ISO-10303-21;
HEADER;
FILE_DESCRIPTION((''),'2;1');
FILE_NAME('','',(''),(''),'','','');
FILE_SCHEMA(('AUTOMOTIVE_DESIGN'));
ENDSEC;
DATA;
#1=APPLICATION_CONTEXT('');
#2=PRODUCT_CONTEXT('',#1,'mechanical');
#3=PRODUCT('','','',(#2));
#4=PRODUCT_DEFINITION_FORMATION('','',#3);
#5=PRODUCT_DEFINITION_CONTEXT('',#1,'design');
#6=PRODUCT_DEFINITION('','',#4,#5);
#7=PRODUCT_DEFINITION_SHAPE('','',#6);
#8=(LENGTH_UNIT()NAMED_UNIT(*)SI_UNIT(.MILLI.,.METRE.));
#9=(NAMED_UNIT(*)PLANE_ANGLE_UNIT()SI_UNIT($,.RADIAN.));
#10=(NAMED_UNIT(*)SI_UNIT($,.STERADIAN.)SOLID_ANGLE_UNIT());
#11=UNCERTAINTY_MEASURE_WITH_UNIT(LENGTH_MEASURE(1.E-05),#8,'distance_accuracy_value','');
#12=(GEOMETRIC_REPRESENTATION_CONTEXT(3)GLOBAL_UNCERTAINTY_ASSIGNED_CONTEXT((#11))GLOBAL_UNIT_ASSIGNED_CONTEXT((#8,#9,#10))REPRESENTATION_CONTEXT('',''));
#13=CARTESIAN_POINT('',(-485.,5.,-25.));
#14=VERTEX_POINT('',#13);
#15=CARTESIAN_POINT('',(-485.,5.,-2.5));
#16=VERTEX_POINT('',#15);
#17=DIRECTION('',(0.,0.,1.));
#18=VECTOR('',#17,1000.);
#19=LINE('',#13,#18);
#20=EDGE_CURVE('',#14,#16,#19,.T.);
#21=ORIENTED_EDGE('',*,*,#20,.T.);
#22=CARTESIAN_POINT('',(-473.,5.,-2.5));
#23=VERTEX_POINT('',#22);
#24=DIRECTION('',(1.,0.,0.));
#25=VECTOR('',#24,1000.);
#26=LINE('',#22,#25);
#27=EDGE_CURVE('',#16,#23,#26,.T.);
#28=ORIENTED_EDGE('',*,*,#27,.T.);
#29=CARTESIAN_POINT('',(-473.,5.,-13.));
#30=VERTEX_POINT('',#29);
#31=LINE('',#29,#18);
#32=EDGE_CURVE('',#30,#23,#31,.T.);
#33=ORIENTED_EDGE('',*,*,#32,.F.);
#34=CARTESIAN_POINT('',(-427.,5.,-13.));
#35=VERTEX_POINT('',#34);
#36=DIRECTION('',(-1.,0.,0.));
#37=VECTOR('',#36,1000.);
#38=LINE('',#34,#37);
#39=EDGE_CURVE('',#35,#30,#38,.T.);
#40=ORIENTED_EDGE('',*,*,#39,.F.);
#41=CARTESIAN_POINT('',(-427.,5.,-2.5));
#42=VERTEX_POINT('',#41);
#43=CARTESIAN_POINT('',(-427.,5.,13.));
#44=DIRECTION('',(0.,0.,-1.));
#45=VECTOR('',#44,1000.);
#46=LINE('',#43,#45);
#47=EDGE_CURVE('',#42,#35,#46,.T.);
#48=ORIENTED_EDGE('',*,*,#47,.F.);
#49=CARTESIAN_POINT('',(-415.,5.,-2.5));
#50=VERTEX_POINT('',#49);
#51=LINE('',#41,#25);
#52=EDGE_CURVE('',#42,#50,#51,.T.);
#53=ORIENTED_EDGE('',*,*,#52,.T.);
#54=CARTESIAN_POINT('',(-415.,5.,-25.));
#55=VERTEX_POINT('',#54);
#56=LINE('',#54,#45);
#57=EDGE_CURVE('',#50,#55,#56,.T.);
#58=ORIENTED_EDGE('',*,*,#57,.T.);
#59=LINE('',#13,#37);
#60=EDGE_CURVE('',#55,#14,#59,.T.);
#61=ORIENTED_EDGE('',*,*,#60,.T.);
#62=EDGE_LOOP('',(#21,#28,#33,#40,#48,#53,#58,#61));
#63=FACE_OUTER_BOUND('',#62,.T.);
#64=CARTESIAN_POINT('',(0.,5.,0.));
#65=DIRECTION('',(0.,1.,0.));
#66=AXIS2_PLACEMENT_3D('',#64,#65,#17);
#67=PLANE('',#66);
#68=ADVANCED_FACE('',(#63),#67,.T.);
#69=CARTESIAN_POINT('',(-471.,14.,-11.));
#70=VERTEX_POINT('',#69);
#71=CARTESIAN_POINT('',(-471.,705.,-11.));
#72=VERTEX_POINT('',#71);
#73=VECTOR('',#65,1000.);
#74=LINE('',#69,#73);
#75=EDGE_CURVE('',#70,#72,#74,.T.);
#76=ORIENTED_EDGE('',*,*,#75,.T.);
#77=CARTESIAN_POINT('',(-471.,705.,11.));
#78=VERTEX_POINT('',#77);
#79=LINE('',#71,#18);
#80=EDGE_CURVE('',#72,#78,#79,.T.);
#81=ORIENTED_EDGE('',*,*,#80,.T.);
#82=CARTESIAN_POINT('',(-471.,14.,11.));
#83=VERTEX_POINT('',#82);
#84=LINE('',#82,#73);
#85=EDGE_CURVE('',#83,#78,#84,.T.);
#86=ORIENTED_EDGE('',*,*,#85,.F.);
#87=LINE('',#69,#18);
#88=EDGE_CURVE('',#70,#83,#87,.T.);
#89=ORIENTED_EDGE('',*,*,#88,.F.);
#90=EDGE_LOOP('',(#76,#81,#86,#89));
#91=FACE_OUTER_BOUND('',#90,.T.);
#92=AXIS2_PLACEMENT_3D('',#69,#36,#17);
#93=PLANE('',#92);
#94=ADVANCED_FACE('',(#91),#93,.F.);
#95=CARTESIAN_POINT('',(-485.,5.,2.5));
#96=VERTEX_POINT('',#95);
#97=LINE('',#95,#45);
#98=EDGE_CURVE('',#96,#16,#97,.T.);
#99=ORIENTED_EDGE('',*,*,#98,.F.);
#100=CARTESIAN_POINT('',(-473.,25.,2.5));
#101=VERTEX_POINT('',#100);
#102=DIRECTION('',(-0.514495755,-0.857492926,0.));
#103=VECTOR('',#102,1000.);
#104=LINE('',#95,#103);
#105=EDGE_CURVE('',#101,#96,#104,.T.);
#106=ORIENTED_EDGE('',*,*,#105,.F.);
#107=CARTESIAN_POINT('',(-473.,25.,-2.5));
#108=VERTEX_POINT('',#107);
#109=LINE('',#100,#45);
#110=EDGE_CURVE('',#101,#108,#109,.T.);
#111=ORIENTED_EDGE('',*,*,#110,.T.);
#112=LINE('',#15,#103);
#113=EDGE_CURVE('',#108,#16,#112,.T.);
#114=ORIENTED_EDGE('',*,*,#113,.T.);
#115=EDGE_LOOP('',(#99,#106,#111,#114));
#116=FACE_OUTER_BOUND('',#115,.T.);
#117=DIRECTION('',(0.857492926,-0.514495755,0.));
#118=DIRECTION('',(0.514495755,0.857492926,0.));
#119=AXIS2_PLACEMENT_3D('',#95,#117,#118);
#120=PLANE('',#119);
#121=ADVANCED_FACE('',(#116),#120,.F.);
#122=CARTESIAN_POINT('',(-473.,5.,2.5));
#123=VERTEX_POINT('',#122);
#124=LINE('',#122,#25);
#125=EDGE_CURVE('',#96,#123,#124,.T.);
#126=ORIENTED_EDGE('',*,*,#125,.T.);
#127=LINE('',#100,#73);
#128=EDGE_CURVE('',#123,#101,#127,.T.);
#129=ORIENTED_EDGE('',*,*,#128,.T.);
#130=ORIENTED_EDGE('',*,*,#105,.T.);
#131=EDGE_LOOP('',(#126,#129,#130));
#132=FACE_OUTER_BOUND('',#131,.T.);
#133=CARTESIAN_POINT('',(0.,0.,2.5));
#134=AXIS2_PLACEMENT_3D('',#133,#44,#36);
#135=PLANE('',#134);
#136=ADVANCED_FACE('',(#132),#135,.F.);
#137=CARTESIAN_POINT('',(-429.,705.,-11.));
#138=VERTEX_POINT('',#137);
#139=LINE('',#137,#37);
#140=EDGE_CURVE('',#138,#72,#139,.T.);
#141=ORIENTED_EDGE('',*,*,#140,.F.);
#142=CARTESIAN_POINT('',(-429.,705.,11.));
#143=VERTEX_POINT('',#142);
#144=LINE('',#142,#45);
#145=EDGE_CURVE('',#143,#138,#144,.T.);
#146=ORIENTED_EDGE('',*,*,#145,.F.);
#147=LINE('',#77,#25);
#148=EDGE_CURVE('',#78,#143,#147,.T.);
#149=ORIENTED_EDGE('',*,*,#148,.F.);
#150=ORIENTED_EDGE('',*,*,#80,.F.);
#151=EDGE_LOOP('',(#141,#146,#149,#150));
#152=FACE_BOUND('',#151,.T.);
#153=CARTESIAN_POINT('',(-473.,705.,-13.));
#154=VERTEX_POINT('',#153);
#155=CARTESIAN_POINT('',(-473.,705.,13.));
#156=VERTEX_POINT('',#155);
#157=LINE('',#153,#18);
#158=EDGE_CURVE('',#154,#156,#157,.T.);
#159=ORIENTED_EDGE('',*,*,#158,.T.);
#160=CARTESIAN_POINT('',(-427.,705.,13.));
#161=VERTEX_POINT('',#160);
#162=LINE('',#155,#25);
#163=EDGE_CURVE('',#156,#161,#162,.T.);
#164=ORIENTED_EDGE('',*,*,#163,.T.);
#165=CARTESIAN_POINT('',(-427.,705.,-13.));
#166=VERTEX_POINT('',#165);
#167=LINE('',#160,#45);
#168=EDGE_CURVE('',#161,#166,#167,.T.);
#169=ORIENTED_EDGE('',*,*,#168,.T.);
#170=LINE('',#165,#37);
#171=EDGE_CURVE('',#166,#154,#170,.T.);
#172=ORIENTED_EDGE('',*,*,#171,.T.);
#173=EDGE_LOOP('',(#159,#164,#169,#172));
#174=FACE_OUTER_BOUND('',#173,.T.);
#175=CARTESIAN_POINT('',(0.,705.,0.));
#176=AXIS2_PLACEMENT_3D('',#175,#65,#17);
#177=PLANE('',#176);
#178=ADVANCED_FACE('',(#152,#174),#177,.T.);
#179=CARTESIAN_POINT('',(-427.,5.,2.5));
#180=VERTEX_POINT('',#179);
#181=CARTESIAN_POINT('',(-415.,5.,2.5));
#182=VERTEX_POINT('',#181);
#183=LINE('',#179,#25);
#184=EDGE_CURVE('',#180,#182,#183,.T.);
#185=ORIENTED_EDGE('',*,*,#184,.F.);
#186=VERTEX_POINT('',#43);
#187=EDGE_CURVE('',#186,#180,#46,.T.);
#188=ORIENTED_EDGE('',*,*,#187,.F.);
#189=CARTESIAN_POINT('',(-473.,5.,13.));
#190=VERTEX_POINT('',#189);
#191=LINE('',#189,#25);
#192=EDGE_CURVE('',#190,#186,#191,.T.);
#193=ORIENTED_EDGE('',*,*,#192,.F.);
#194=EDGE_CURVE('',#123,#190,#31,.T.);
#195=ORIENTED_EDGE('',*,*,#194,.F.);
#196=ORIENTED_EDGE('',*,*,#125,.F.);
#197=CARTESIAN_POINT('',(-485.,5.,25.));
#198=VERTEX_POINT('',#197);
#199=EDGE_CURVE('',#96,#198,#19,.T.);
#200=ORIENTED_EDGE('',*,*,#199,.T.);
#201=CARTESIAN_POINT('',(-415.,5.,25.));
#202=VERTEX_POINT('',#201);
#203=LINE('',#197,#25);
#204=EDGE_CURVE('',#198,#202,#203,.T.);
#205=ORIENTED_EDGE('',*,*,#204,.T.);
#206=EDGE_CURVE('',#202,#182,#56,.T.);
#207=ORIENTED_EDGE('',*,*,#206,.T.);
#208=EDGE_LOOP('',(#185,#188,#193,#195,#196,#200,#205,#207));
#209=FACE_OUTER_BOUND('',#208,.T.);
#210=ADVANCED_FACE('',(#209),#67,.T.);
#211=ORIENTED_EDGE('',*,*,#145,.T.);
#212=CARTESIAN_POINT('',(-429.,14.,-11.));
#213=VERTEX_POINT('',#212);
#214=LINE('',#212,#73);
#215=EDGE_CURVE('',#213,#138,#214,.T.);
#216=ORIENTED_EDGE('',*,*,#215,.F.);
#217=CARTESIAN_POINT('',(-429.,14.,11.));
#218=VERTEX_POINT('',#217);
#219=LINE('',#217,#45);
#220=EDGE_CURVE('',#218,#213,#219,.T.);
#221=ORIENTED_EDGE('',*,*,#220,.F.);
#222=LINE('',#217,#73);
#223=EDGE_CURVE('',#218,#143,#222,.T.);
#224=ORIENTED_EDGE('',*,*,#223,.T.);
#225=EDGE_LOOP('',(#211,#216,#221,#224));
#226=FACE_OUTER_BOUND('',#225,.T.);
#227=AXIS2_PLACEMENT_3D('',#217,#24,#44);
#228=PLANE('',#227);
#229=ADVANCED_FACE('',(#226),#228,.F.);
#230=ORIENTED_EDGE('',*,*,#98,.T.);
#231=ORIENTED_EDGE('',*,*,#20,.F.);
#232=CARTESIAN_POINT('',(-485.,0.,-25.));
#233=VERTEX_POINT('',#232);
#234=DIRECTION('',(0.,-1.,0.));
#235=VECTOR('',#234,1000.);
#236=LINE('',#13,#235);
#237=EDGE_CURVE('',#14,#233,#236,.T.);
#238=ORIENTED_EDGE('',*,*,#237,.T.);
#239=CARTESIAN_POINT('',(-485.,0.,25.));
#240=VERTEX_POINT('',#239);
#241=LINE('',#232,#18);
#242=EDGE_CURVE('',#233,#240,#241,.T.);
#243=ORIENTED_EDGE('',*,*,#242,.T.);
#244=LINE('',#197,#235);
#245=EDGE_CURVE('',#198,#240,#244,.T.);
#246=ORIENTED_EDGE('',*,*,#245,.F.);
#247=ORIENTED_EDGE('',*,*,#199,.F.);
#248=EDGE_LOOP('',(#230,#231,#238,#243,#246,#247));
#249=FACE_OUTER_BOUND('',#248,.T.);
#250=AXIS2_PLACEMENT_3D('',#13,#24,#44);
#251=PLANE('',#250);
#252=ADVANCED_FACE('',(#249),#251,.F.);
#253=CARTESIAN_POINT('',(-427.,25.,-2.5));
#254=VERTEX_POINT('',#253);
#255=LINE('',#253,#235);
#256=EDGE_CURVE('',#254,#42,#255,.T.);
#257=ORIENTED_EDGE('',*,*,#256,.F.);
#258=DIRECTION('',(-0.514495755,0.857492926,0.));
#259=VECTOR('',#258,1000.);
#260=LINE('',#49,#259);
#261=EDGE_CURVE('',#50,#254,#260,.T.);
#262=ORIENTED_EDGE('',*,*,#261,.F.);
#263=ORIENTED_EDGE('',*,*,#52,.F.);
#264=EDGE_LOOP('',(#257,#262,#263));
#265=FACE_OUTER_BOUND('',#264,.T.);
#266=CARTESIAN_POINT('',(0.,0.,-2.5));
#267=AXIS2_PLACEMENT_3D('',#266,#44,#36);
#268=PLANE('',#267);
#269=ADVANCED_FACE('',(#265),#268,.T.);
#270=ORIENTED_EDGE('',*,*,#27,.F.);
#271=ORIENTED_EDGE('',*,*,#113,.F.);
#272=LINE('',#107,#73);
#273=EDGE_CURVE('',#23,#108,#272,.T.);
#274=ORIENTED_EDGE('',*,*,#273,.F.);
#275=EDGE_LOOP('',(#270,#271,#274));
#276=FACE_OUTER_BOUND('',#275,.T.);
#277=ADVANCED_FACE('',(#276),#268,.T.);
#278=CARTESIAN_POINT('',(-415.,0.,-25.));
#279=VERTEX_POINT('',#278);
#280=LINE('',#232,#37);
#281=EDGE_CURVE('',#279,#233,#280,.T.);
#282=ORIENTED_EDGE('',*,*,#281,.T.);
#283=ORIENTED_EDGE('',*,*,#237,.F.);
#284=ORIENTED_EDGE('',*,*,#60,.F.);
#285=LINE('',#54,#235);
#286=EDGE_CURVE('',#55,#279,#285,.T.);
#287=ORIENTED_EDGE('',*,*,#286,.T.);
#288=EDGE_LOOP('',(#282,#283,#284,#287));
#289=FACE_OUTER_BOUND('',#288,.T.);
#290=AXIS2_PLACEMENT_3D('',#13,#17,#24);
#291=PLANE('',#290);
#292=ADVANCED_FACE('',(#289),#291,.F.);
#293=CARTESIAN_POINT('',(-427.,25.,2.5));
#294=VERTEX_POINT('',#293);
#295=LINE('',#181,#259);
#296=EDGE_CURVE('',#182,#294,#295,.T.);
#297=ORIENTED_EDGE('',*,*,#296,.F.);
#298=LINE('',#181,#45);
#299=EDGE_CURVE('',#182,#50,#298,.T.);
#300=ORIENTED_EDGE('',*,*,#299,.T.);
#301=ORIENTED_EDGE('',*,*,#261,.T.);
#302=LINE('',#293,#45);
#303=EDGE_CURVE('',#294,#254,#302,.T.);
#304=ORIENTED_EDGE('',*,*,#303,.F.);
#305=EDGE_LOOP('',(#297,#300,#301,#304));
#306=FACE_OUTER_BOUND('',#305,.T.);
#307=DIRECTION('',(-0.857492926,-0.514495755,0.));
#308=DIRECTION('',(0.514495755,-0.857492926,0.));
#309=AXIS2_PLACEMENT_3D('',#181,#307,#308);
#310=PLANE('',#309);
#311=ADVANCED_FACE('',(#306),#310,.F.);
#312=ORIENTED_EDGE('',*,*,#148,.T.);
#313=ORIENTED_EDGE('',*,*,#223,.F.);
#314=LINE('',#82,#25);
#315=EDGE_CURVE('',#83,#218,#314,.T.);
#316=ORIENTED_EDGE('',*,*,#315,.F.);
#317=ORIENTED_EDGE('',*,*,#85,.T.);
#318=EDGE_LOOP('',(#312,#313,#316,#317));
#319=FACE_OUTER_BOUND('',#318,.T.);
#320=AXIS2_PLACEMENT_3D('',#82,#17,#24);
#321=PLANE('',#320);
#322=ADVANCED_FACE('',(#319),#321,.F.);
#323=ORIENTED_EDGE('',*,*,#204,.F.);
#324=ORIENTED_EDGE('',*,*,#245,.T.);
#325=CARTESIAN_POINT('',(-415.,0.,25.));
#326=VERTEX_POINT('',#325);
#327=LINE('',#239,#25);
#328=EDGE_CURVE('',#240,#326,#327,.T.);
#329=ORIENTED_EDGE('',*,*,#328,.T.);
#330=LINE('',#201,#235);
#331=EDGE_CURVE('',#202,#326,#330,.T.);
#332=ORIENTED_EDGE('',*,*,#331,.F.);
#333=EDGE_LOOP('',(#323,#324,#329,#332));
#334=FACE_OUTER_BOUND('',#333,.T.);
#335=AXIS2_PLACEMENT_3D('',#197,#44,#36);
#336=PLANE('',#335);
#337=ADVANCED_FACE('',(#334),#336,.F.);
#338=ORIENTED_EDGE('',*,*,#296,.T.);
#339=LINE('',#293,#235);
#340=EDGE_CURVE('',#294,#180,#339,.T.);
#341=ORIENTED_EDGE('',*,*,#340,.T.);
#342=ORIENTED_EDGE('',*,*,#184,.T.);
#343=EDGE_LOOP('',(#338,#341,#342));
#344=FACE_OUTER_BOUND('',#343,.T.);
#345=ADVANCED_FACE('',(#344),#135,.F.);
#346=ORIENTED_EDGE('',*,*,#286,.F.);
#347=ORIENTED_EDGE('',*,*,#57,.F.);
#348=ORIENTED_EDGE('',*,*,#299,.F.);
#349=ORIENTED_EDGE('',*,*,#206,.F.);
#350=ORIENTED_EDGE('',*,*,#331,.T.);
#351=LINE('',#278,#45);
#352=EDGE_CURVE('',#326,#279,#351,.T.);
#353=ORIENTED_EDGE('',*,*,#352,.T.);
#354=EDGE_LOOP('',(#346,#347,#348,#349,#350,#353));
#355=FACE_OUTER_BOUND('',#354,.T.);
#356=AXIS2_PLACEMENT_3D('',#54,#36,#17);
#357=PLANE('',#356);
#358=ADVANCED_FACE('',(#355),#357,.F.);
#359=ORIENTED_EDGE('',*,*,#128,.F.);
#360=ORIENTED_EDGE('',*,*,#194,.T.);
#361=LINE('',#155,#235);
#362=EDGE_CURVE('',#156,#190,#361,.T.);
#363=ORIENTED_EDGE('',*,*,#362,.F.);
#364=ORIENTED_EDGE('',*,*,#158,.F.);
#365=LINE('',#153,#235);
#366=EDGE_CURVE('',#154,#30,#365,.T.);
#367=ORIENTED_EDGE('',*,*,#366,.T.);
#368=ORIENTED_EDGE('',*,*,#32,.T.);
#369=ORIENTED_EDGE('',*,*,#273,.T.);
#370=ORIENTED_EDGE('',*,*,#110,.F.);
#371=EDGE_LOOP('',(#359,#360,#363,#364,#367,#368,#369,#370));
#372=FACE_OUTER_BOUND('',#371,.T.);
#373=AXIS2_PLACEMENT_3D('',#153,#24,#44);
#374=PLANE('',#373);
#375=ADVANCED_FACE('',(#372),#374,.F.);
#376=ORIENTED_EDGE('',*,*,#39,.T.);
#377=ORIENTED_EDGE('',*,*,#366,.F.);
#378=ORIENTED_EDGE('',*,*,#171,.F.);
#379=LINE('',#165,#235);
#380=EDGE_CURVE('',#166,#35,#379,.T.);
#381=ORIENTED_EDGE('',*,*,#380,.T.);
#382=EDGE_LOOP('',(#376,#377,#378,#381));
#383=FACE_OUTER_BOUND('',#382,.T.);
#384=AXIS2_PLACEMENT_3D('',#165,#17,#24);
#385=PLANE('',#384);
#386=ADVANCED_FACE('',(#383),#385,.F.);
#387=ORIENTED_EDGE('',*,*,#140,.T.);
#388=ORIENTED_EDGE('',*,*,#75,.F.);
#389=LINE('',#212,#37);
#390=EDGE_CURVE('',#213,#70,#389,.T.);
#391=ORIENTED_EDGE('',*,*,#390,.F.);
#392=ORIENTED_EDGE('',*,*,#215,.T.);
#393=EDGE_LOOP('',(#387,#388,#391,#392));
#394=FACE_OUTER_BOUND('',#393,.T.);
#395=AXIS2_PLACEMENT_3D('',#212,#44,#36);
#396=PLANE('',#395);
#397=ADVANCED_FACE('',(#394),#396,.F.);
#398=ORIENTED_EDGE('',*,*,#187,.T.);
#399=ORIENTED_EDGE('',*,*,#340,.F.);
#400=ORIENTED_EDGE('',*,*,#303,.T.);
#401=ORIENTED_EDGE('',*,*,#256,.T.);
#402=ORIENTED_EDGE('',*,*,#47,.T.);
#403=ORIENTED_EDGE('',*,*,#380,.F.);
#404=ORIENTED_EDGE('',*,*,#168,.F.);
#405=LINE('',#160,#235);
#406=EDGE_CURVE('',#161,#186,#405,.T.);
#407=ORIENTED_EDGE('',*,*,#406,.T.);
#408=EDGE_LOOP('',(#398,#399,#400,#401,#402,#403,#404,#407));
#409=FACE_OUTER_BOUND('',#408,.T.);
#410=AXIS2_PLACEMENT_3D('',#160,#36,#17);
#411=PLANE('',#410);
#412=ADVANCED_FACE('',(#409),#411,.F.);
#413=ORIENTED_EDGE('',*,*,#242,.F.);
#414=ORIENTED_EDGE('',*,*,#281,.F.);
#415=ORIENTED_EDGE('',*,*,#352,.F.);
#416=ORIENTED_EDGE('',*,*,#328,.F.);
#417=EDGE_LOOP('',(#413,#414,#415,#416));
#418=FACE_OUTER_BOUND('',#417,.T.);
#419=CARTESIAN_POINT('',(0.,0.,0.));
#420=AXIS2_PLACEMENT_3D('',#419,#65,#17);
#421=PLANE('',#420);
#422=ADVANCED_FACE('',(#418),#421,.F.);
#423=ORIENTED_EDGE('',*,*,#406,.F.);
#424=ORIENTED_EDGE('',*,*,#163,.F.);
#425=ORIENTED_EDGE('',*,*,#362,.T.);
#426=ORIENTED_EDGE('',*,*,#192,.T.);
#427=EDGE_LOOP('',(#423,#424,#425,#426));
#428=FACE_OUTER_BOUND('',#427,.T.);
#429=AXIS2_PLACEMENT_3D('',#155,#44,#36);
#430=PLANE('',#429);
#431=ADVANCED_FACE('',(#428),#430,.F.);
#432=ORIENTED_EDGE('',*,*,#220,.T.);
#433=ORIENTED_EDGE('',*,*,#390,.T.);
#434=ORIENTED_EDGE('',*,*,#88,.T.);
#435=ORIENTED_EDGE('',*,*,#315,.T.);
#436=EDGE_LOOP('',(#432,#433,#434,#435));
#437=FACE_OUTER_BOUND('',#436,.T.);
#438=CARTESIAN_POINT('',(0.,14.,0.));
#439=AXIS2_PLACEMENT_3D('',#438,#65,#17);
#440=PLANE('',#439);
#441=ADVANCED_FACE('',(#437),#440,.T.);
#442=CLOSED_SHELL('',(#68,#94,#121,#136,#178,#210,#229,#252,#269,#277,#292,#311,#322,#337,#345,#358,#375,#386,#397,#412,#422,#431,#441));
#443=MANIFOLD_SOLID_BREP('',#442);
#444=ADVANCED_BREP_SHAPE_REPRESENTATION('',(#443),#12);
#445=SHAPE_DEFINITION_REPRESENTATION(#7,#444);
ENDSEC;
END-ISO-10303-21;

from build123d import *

# Parameters (mm, degrees)
SKETCH2_W           = 70
SKETCH2_H           = 50
BOSS_EXTRUDE1_DEPTH = 5
SKETCH3_W           = 46
SKETCH3_H           = 26
BOSS_EXTRUDE2_DEPTH = 700
BOSS_EXTRUDE3_DEPTH = 2.5
SKETCH5_W           = 42
SKETCH5_H           = 22
CUT_EXTRUDE1_DEPTH  = 691


with BuildPart() as part:
    # Sketch2 → Boss-Extrude1 (new body)
    with BuildSketch(Plane(origin=(0, 0, 0), x_dir=(1, 0, 0), z_dir=(0, 1, 0))):
        with Locations((-450, 0)):
            Rectangle(SKETCH2_W, SKETCH2_H)
    extrude(amount=BOSS_EXTRUDE1_DEPTH)

    # Sketch3 → Boss-Extrude2 (add)
    with BuildSketch(Plane(origin=(0, 5, 0), x_dir=(1, 0, 0), z_dir=(0, 1, 0))):
        with Locations((-450, 0)):
            Rectangle(SKETCH3_W, SKETCH3_H)
    extrude(amount=BOSS_EXTRUDE2_DEPTH)

    # Sketch4 → Boss-Extrude3 (add, symmetric)
    with BuildSketch(Plane.XY):
        Polygon((-473, 5), (-485, 5), (-473, 25), align=None)
        Polygon((-427, 25), (-427, 5), (-415, 5), align=None)
    extrude(amount=BOSS_EXTRUDE3_DEPTH, both=True)

    # Sketch5 → Cut-Extrude1 (cut)
    with BuildSketch(Plane(origin=(0, 705, 0), x_dir=(1, 0, 0), z_dir=(0, 1, 0))):
        with Locations((-450, 0)):
            Rectangle(SKETCH5_W, SKETCH5_H)
    extrude(amount=-CUT_EXTRUDE1_DEPTH, mode=Mode.SUBTRACT)


solid = part.part
